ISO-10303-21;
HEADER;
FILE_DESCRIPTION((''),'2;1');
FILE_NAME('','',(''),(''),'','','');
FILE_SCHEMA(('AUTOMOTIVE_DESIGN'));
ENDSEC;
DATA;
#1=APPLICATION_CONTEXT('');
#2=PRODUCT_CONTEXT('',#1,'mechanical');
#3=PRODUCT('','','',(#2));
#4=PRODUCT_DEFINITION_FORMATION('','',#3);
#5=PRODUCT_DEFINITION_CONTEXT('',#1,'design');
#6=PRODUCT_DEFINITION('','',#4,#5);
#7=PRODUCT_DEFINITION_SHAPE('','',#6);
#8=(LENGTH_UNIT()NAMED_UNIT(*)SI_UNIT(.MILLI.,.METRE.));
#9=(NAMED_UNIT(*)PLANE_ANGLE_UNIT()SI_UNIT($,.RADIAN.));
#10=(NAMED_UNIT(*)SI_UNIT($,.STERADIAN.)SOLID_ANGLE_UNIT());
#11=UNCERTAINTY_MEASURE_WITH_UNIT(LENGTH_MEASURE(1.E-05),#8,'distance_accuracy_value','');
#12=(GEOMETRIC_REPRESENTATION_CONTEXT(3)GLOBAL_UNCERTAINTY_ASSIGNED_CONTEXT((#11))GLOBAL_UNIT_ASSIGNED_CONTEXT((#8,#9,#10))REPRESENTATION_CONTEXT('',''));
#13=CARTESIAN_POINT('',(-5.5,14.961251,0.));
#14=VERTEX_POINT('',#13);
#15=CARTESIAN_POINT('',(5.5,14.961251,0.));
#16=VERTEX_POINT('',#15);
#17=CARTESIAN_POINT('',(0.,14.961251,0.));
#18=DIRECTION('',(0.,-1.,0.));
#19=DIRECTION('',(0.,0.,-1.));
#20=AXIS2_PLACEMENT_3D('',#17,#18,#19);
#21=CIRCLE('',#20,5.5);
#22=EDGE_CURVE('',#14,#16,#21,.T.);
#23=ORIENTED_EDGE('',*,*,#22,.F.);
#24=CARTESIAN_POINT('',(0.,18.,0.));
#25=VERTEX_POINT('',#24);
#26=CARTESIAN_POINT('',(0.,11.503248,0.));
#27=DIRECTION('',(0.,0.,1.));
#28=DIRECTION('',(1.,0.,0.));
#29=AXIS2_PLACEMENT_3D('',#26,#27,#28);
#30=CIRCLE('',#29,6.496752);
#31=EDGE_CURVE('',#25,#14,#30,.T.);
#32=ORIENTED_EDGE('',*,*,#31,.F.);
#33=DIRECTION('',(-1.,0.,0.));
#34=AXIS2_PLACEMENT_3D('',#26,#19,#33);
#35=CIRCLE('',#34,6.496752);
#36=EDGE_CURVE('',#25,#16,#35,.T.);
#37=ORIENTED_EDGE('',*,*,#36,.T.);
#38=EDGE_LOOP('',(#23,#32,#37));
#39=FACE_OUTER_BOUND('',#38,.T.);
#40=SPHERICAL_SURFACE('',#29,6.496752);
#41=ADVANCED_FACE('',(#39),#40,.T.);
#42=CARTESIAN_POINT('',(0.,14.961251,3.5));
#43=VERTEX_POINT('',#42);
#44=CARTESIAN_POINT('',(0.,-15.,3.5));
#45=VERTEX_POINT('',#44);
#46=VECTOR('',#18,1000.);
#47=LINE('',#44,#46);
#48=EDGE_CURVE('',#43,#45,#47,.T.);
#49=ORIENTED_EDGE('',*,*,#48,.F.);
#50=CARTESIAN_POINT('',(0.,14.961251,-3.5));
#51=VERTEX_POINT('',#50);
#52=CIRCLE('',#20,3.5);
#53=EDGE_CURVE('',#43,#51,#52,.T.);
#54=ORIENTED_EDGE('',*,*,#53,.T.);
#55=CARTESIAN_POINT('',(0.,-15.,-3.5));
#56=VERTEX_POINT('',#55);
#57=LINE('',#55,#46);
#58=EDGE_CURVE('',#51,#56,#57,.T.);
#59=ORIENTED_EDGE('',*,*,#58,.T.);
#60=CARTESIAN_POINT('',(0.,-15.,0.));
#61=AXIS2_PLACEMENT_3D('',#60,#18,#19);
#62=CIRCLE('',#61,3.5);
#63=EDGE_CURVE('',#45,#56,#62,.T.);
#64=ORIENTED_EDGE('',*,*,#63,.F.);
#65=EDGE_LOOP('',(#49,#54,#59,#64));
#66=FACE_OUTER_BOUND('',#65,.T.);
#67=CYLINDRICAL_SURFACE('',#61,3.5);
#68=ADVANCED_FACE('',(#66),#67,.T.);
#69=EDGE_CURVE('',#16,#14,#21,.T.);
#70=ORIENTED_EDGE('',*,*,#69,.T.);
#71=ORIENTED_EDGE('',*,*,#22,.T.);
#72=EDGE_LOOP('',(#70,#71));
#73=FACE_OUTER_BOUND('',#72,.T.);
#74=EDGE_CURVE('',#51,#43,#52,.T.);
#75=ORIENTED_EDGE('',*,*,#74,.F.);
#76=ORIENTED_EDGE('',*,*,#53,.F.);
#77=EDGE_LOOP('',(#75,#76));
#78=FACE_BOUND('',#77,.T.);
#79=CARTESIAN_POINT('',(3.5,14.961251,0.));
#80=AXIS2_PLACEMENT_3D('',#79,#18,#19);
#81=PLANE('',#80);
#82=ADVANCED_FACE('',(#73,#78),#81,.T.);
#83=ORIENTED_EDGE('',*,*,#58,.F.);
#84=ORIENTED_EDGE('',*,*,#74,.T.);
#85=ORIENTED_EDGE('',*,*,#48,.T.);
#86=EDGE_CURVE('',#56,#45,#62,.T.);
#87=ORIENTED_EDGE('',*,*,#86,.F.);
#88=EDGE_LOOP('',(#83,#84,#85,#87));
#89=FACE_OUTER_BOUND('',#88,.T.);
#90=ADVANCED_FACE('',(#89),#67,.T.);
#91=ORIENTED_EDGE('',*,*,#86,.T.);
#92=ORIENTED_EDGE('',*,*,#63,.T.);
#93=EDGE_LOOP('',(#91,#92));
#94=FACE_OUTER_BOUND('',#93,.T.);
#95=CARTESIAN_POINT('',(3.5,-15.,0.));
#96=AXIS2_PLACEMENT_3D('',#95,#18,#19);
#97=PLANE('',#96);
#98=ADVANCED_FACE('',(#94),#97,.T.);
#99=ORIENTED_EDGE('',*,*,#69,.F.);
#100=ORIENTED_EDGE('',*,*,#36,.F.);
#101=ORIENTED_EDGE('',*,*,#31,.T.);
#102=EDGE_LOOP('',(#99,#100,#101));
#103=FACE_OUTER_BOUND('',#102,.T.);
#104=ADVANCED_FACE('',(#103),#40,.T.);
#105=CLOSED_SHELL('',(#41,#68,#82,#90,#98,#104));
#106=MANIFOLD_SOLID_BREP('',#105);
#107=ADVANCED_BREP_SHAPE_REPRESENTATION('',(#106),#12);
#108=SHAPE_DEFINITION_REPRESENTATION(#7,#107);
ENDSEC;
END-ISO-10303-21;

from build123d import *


with BuildPart() as part:
    # 草图1 → 旋转1 (revolve)
    with BuildSketch(Plane.XY, mode=Mode.PRIVATE) as revolve_1_sk:
        with BuildLine():
            Line((0, -15), (0, 15))
            Line((0, 15), (0, 18))
            ThreePointArc((0, 18), (3.141814541, 17.18979245), (5.5, 14.961251172))
            Line((5.5, 14.961251172), (3.5, 14.961251172))
            Line((3.5, 14.961251172), (3.5, -15))
            Line((3.5, -15), (0, -15))
        make_face()
    revolve(revolve_1_sk.sketch.rotate(Axis((0, -15, 0), (0, 1, 0)), 90), axis=Axis((0, -15, 0), (0, 1, 0)))


solid = part.part
